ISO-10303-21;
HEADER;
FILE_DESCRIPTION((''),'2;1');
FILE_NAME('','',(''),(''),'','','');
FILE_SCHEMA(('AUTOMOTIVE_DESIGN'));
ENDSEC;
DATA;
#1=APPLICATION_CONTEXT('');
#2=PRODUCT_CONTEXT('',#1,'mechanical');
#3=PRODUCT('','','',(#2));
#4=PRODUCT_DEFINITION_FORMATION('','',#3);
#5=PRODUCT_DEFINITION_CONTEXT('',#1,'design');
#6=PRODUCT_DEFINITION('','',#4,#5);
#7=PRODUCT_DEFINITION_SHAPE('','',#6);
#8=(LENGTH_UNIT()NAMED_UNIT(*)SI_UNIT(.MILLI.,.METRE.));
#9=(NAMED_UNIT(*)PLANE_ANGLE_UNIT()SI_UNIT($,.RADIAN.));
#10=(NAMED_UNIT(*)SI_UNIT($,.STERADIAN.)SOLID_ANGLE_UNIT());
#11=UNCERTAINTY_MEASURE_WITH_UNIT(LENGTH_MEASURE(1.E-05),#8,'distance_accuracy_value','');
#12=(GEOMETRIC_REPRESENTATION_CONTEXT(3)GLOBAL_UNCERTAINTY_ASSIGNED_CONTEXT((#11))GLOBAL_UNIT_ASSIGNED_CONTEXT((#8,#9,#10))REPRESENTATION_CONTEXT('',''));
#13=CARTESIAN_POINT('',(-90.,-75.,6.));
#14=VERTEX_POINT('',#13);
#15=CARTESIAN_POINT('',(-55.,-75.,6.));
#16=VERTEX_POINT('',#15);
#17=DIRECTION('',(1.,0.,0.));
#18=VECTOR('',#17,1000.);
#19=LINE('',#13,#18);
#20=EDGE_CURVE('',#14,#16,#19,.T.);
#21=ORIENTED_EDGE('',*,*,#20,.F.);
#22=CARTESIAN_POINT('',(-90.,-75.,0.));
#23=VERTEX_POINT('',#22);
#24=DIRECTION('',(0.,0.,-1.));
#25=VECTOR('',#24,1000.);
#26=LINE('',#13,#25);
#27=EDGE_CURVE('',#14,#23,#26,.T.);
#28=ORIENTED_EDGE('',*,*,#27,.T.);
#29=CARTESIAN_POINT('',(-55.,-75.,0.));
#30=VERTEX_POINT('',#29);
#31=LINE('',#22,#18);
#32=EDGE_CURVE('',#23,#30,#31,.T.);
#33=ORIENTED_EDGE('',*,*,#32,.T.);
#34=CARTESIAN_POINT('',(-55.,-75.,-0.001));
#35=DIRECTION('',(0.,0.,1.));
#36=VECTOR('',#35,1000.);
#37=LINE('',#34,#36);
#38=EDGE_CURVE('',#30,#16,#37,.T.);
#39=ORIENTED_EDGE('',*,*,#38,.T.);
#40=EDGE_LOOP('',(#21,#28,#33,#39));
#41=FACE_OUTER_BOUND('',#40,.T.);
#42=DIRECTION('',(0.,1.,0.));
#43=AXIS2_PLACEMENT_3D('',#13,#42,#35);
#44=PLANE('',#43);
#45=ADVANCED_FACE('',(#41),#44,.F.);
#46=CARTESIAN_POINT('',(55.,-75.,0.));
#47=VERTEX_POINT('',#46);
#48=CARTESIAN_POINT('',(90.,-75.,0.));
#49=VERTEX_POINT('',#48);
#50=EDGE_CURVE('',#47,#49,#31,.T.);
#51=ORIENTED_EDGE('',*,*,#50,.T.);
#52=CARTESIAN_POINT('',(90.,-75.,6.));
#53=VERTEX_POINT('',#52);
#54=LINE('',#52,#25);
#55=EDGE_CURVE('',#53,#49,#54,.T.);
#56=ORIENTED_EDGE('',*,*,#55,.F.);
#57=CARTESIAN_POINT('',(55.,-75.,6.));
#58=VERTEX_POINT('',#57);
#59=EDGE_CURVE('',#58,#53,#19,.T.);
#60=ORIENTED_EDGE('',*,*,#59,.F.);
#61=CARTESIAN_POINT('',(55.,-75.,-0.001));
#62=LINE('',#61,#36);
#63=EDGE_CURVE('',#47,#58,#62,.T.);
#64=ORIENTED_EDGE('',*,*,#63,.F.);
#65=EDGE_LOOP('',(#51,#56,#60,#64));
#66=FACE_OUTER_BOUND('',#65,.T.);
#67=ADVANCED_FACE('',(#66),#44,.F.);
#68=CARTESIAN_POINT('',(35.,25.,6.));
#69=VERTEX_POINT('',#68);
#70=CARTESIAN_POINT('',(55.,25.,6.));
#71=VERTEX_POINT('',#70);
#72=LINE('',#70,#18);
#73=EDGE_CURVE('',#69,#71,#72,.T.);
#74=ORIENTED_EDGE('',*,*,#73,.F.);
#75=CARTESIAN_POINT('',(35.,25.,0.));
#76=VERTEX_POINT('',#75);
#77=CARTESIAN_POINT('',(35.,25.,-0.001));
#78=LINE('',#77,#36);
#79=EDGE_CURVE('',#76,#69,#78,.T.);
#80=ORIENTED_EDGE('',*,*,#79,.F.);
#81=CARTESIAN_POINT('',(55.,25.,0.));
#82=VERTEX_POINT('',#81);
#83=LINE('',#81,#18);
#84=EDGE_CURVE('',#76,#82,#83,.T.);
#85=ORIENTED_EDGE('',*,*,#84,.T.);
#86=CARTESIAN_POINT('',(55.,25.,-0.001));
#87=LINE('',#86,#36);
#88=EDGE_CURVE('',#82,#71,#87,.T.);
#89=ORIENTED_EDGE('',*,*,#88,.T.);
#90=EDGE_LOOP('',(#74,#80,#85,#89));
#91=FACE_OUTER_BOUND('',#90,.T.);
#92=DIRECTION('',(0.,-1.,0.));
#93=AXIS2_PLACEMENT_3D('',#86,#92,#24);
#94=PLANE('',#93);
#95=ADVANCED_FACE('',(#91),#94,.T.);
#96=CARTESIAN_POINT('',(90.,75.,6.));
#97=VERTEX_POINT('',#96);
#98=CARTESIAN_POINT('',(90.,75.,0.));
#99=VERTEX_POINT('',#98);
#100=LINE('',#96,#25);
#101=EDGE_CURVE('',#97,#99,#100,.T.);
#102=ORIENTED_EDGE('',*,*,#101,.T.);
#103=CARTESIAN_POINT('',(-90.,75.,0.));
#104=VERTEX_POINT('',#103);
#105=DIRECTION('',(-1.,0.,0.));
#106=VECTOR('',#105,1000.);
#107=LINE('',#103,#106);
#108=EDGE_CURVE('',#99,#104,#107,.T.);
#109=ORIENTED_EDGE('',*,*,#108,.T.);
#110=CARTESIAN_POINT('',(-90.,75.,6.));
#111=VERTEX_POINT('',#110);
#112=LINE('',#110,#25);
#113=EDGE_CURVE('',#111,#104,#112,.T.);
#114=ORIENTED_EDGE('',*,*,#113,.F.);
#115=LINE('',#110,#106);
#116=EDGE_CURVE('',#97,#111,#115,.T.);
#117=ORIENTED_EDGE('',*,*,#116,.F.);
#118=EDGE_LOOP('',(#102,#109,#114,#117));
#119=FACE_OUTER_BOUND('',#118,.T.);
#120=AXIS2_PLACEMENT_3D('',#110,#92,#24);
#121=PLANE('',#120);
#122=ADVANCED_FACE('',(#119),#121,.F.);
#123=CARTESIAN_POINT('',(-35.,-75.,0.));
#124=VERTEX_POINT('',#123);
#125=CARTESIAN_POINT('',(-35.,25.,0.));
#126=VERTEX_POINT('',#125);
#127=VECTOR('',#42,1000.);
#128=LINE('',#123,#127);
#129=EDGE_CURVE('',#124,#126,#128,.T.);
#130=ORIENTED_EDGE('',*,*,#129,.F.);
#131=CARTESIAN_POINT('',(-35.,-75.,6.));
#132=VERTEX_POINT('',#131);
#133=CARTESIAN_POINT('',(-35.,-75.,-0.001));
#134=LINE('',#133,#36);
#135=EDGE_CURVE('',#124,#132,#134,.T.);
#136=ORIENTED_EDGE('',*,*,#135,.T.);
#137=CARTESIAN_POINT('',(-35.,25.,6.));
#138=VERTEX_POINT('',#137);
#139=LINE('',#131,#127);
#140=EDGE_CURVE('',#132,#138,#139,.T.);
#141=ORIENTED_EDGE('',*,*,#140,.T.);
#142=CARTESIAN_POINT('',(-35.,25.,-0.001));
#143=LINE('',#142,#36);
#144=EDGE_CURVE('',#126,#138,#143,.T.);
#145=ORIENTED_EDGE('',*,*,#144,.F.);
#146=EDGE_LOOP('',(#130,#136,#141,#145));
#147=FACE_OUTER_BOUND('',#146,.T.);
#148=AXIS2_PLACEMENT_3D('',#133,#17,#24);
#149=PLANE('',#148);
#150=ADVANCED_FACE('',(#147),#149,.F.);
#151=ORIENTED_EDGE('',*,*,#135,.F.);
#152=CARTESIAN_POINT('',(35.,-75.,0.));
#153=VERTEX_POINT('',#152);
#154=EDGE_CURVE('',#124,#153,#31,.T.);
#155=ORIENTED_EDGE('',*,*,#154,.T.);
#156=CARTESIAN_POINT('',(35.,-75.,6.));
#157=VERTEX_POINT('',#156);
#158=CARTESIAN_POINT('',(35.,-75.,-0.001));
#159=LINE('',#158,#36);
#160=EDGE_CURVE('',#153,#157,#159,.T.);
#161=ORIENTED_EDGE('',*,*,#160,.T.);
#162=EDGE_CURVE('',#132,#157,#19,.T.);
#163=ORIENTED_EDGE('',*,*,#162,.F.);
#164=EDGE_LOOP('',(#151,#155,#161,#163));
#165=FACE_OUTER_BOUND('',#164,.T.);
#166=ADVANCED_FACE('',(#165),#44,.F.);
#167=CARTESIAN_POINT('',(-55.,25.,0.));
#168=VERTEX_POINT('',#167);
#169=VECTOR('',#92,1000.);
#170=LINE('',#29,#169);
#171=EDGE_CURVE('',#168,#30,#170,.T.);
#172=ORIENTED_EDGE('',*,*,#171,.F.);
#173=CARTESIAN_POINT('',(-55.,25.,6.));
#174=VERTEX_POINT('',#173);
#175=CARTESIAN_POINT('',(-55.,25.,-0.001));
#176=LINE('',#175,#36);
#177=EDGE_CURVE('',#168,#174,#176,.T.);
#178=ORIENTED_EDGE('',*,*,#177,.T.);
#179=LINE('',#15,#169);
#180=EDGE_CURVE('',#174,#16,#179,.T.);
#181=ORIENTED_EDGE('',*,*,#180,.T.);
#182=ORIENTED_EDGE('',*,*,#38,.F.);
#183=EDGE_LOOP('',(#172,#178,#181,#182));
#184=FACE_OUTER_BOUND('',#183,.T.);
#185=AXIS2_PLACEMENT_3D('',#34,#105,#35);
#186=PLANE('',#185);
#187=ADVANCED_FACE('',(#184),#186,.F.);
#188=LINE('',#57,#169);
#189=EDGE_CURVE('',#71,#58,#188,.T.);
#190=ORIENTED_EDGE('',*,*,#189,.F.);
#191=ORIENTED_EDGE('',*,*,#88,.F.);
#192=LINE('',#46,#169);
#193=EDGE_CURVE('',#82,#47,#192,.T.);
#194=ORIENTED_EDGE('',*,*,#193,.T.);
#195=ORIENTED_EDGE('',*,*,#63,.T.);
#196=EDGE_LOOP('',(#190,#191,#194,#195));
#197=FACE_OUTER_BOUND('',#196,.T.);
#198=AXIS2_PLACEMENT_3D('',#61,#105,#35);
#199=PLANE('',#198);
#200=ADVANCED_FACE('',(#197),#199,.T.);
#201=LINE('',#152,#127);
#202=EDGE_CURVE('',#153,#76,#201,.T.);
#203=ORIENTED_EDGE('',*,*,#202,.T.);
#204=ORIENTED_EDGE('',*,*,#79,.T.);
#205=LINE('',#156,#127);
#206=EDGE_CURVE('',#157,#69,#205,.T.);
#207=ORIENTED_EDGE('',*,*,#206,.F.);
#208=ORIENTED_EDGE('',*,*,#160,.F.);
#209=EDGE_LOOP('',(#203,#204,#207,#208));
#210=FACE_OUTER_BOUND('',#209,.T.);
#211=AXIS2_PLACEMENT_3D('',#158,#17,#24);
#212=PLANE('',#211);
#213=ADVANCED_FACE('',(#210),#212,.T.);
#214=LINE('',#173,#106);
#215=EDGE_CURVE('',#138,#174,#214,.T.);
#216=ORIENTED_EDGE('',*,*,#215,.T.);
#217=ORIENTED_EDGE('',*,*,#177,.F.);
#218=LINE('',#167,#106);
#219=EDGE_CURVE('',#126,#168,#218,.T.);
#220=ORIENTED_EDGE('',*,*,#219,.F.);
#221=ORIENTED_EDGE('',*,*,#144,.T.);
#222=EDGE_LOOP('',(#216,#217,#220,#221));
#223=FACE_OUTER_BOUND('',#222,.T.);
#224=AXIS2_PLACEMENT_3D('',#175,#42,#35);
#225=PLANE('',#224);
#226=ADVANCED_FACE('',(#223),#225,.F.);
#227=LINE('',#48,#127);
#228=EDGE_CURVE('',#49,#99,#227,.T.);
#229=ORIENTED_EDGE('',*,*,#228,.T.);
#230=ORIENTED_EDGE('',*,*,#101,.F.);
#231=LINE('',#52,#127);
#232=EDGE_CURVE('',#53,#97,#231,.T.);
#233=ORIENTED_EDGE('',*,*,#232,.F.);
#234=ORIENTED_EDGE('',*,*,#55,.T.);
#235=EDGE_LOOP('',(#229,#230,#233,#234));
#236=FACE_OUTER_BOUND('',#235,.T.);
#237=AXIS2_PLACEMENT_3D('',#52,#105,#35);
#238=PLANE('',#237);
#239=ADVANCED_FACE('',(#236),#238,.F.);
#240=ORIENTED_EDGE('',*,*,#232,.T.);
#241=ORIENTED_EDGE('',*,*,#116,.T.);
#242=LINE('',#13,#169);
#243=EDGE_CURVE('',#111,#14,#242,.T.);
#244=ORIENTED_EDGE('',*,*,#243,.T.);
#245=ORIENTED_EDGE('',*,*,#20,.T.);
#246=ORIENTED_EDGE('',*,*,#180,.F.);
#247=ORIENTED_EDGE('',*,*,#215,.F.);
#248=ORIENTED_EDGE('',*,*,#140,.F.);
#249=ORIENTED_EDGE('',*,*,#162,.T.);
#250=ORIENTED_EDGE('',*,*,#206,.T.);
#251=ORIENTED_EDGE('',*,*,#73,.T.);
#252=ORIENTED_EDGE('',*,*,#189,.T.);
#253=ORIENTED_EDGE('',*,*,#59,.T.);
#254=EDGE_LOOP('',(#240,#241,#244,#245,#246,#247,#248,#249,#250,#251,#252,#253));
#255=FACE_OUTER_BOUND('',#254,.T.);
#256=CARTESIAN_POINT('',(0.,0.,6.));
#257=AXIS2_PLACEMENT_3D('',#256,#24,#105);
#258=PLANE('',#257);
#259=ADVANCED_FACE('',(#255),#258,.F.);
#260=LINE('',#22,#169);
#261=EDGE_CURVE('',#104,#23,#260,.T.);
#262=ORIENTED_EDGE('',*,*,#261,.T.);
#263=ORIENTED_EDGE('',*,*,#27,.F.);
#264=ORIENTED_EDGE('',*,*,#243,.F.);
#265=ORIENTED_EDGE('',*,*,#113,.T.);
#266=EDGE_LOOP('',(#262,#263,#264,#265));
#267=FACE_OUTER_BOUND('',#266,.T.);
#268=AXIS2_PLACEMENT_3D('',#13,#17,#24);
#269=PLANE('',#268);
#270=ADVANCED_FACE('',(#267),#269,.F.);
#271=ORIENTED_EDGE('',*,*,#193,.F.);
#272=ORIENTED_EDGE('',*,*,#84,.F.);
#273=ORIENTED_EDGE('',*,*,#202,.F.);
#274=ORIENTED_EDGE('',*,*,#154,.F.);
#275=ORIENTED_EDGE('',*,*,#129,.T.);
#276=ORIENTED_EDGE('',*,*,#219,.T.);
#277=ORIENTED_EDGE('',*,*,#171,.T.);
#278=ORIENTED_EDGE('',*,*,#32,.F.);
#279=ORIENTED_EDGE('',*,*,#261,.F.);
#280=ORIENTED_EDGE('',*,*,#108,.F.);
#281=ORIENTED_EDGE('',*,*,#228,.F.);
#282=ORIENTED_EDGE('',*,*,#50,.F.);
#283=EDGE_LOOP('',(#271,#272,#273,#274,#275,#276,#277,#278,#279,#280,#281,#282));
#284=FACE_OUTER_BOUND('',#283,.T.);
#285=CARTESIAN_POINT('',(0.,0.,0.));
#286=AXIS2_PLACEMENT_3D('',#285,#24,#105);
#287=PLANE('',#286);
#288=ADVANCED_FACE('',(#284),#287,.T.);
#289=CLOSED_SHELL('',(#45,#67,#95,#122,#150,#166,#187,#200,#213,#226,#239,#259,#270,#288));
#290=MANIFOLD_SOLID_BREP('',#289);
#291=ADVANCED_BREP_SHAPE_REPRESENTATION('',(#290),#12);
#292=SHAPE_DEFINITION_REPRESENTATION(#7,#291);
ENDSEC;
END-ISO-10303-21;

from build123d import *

# Parameters (mm, degrees)
SKETCH_1_W          = 180
SKETCH_1_H          = 150
EXTRUDE_1_DEPTH     = 6
CUT_EXTRUDE_1_REACH = 119.307
SKETCH_2_W          = 20
SKETCH_2_H          = 100


with BuildPart() as part:
    # 草图1 → 凸台-拉伸1 (new body)
    with BuildSketch(Plane.XY):
        Rectangle(SKETCH_1_W, SKETCH_1_H)
    extrude(amount=EXTRUDE_1_DEPTH)

    # 草图2 → 切除-拉伸1 (cut, up to next)
    with BuildSketch(Plane.XY.offset(6), mode=Mode.PRIVATE) as cut_extrude_1_sk1:
        with Locations((-45, -25)):
            Rectangle(SKETCH_2_W, SKETCH_2_H)
    cut_extrude_1_tool1 = extrude(cut_extrude_1_sk1.sketch, amount=-CUT_EXTRUDE_1_REACH, mode=Mode.PRIVATE) & part.part
    cut_extrude_1 = cut_extrude_1_tool1.solids().sort_by_distance((-45, -25, 6))[0]
    add(cut_extrude_1, mode=Mode.SUBTRACT)

    # 镜向1: 切除-拉伸1 across plane
    add(cut_extrude_1.mirror(Plane(origin=(0, 0, 0), x_dir=(0, 0, 1), z_dir=(1, 0, 0))), mode=Mode.SUBTRACT)


solid = part.part
